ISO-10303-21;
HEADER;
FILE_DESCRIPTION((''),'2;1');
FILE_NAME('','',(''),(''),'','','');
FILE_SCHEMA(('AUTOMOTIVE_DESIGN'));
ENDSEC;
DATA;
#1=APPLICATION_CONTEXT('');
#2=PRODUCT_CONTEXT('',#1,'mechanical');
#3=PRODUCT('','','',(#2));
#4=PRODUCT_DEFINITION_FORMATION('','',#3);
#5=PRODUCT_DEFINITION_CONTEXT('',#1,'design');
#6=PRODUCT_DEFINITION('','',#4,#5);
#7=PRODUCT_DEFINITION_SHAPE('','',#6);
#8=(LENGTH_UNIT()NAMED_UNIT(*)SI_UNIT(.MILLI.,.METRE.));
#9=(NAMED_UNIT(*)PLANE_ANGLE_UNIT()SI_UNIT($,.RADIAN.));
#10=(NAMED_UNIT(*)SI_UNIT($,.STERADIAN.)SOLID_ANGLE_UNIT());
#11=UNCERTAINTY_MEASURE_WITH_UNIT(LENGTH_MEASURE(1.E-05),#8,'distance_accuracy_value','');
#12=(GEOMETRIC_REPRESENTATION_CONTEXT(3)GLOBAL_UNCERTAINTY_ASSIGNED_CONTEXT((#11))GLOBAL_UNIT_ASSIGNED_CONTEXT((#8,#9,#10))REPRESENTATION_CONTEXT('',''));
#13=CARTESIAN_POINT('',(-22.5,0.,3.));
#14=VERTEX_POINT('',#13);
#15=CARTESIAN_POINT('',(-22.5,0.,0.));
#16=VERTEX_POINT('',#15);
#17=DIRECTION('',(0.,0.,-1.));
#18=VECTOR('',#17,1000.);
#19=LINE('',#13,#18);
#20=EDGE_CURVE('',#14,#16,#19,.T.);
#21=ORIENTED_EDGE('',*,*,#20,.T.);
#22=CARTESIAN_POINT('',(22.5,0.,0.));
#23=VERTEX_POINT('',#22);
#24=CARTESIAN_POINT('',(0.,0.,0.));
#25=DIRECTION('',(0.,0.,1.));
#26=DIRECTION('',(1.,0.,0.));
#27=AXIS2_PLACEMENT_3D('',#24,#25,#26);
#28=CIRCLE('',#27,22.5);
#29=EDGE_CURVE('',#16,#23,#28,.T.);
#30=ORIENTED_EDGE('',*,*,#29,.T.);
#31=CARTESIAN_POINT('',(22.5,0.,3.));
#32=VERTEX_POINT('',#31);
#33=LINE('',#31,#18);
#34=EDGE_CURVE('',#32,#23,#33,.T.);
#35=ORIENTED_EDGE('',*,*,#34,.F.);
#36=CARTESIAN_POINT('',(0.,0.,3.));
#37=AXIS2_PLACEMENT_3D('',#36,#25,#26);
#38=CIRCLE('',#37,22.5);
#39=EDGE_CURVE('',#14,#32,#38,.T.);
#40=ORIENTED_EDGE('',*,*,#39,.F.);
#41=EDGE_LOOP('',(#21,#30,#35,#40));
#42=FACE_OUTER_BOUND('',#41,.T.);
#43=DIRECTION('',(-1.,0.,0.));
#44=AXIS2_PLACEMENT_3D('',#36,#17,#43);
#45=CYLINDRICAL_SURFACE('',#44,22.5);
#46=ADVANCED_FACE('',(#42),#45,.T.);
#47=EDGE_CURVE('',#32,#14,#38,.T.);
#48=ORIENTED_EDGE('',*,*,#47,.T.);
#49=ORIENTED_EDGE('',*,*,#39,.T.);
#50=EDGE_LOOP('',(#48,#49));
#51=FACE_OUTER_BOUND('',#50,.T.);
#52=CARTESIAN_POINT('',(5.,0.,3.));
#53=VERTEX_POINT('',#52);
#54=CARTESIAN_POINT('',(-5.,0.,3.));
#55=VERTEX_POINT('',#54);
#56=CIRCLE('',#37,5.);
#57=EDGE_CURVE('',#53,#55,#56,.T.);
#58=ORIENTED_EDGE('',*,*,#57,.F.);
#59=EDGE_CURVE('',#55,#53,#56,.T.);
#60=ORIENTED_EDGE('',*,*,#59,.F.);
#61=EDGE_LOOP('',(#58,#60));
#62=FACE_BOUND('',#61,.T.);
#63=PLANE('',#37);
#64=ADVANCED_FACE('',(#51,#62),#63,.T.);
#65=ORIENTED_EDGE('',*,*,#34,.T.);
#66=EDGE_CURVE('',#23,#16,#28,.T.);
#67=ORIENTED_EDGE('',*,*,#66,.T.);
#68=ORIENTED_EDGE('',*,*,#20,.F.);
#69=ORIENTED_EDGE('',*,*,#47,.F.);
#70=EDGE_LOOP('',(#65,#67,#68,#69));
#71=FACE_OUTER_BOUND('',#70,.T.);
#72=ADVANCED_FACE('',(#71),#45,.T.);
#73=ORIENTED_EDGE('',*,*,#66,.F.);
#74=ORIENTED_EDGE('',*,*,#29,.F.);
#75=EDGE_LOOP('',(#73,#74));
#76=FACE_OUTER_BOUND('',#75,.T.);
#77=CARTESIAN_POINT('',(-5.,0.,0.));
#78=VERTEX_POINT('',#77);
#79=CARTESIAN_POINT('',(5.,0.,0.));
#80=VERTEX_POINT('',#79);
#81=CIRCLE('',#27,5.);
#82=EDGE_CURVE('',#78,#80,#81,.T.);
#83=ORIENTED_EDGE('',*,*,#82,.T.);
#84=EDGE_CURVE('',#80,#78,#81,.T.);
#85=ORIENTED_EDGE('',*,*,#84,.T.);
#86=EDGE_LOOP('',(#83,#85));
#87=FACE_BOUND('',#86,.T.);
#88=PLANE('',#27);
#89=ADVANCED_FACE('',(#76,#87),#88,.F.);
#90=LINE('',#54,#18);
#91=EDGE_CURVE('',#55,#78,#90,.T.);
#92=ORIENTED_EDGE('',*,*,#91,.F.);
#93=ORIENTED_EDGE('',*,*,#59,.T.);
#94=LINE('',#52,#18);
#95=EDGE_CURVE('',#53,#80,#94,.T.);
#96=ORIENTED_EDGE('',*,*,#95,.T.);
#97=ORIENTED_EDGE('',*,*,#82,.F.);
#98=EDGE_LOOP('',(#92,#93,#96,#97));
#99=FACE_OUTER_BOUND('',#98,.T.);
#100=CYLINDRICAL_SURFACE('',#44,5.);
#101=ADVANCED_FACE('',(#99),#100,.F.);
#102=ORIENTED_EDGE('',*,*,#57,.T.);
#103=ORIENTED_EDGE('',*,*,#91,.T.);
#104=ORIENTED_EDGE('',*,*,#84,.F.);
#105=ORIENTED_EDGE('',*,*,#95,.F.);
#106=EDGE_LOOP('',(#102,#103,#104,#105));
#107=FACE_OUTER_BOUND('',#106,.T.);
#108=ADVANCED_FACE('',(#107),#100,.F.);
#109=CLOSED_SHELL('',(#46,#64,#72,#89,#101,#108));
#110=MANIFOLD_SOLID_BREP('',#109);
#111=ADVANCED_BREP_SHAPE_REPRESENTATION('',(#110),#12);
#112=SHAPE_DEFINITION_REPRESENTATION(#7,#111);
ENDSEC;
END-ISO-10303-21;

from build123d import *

# Parameters (mm, degrees)
SKETCH_1_R      = 22.5
SKETCH_1_R_2    = 5
EXTRUDE_1_DEPTH = 3


with BuildPart() as part:
    # 草图1 → 凸台-拉伸1 (new body)
    with BuildSketch(Plane.XY):
        Circle(SKETCH_1_R)
        Circle(SKETCH_1_R_2, mode=Mode.SUBTRACT)
    extrude(amount=EXTRUDE_1_DEPTH)


solid = part.part
